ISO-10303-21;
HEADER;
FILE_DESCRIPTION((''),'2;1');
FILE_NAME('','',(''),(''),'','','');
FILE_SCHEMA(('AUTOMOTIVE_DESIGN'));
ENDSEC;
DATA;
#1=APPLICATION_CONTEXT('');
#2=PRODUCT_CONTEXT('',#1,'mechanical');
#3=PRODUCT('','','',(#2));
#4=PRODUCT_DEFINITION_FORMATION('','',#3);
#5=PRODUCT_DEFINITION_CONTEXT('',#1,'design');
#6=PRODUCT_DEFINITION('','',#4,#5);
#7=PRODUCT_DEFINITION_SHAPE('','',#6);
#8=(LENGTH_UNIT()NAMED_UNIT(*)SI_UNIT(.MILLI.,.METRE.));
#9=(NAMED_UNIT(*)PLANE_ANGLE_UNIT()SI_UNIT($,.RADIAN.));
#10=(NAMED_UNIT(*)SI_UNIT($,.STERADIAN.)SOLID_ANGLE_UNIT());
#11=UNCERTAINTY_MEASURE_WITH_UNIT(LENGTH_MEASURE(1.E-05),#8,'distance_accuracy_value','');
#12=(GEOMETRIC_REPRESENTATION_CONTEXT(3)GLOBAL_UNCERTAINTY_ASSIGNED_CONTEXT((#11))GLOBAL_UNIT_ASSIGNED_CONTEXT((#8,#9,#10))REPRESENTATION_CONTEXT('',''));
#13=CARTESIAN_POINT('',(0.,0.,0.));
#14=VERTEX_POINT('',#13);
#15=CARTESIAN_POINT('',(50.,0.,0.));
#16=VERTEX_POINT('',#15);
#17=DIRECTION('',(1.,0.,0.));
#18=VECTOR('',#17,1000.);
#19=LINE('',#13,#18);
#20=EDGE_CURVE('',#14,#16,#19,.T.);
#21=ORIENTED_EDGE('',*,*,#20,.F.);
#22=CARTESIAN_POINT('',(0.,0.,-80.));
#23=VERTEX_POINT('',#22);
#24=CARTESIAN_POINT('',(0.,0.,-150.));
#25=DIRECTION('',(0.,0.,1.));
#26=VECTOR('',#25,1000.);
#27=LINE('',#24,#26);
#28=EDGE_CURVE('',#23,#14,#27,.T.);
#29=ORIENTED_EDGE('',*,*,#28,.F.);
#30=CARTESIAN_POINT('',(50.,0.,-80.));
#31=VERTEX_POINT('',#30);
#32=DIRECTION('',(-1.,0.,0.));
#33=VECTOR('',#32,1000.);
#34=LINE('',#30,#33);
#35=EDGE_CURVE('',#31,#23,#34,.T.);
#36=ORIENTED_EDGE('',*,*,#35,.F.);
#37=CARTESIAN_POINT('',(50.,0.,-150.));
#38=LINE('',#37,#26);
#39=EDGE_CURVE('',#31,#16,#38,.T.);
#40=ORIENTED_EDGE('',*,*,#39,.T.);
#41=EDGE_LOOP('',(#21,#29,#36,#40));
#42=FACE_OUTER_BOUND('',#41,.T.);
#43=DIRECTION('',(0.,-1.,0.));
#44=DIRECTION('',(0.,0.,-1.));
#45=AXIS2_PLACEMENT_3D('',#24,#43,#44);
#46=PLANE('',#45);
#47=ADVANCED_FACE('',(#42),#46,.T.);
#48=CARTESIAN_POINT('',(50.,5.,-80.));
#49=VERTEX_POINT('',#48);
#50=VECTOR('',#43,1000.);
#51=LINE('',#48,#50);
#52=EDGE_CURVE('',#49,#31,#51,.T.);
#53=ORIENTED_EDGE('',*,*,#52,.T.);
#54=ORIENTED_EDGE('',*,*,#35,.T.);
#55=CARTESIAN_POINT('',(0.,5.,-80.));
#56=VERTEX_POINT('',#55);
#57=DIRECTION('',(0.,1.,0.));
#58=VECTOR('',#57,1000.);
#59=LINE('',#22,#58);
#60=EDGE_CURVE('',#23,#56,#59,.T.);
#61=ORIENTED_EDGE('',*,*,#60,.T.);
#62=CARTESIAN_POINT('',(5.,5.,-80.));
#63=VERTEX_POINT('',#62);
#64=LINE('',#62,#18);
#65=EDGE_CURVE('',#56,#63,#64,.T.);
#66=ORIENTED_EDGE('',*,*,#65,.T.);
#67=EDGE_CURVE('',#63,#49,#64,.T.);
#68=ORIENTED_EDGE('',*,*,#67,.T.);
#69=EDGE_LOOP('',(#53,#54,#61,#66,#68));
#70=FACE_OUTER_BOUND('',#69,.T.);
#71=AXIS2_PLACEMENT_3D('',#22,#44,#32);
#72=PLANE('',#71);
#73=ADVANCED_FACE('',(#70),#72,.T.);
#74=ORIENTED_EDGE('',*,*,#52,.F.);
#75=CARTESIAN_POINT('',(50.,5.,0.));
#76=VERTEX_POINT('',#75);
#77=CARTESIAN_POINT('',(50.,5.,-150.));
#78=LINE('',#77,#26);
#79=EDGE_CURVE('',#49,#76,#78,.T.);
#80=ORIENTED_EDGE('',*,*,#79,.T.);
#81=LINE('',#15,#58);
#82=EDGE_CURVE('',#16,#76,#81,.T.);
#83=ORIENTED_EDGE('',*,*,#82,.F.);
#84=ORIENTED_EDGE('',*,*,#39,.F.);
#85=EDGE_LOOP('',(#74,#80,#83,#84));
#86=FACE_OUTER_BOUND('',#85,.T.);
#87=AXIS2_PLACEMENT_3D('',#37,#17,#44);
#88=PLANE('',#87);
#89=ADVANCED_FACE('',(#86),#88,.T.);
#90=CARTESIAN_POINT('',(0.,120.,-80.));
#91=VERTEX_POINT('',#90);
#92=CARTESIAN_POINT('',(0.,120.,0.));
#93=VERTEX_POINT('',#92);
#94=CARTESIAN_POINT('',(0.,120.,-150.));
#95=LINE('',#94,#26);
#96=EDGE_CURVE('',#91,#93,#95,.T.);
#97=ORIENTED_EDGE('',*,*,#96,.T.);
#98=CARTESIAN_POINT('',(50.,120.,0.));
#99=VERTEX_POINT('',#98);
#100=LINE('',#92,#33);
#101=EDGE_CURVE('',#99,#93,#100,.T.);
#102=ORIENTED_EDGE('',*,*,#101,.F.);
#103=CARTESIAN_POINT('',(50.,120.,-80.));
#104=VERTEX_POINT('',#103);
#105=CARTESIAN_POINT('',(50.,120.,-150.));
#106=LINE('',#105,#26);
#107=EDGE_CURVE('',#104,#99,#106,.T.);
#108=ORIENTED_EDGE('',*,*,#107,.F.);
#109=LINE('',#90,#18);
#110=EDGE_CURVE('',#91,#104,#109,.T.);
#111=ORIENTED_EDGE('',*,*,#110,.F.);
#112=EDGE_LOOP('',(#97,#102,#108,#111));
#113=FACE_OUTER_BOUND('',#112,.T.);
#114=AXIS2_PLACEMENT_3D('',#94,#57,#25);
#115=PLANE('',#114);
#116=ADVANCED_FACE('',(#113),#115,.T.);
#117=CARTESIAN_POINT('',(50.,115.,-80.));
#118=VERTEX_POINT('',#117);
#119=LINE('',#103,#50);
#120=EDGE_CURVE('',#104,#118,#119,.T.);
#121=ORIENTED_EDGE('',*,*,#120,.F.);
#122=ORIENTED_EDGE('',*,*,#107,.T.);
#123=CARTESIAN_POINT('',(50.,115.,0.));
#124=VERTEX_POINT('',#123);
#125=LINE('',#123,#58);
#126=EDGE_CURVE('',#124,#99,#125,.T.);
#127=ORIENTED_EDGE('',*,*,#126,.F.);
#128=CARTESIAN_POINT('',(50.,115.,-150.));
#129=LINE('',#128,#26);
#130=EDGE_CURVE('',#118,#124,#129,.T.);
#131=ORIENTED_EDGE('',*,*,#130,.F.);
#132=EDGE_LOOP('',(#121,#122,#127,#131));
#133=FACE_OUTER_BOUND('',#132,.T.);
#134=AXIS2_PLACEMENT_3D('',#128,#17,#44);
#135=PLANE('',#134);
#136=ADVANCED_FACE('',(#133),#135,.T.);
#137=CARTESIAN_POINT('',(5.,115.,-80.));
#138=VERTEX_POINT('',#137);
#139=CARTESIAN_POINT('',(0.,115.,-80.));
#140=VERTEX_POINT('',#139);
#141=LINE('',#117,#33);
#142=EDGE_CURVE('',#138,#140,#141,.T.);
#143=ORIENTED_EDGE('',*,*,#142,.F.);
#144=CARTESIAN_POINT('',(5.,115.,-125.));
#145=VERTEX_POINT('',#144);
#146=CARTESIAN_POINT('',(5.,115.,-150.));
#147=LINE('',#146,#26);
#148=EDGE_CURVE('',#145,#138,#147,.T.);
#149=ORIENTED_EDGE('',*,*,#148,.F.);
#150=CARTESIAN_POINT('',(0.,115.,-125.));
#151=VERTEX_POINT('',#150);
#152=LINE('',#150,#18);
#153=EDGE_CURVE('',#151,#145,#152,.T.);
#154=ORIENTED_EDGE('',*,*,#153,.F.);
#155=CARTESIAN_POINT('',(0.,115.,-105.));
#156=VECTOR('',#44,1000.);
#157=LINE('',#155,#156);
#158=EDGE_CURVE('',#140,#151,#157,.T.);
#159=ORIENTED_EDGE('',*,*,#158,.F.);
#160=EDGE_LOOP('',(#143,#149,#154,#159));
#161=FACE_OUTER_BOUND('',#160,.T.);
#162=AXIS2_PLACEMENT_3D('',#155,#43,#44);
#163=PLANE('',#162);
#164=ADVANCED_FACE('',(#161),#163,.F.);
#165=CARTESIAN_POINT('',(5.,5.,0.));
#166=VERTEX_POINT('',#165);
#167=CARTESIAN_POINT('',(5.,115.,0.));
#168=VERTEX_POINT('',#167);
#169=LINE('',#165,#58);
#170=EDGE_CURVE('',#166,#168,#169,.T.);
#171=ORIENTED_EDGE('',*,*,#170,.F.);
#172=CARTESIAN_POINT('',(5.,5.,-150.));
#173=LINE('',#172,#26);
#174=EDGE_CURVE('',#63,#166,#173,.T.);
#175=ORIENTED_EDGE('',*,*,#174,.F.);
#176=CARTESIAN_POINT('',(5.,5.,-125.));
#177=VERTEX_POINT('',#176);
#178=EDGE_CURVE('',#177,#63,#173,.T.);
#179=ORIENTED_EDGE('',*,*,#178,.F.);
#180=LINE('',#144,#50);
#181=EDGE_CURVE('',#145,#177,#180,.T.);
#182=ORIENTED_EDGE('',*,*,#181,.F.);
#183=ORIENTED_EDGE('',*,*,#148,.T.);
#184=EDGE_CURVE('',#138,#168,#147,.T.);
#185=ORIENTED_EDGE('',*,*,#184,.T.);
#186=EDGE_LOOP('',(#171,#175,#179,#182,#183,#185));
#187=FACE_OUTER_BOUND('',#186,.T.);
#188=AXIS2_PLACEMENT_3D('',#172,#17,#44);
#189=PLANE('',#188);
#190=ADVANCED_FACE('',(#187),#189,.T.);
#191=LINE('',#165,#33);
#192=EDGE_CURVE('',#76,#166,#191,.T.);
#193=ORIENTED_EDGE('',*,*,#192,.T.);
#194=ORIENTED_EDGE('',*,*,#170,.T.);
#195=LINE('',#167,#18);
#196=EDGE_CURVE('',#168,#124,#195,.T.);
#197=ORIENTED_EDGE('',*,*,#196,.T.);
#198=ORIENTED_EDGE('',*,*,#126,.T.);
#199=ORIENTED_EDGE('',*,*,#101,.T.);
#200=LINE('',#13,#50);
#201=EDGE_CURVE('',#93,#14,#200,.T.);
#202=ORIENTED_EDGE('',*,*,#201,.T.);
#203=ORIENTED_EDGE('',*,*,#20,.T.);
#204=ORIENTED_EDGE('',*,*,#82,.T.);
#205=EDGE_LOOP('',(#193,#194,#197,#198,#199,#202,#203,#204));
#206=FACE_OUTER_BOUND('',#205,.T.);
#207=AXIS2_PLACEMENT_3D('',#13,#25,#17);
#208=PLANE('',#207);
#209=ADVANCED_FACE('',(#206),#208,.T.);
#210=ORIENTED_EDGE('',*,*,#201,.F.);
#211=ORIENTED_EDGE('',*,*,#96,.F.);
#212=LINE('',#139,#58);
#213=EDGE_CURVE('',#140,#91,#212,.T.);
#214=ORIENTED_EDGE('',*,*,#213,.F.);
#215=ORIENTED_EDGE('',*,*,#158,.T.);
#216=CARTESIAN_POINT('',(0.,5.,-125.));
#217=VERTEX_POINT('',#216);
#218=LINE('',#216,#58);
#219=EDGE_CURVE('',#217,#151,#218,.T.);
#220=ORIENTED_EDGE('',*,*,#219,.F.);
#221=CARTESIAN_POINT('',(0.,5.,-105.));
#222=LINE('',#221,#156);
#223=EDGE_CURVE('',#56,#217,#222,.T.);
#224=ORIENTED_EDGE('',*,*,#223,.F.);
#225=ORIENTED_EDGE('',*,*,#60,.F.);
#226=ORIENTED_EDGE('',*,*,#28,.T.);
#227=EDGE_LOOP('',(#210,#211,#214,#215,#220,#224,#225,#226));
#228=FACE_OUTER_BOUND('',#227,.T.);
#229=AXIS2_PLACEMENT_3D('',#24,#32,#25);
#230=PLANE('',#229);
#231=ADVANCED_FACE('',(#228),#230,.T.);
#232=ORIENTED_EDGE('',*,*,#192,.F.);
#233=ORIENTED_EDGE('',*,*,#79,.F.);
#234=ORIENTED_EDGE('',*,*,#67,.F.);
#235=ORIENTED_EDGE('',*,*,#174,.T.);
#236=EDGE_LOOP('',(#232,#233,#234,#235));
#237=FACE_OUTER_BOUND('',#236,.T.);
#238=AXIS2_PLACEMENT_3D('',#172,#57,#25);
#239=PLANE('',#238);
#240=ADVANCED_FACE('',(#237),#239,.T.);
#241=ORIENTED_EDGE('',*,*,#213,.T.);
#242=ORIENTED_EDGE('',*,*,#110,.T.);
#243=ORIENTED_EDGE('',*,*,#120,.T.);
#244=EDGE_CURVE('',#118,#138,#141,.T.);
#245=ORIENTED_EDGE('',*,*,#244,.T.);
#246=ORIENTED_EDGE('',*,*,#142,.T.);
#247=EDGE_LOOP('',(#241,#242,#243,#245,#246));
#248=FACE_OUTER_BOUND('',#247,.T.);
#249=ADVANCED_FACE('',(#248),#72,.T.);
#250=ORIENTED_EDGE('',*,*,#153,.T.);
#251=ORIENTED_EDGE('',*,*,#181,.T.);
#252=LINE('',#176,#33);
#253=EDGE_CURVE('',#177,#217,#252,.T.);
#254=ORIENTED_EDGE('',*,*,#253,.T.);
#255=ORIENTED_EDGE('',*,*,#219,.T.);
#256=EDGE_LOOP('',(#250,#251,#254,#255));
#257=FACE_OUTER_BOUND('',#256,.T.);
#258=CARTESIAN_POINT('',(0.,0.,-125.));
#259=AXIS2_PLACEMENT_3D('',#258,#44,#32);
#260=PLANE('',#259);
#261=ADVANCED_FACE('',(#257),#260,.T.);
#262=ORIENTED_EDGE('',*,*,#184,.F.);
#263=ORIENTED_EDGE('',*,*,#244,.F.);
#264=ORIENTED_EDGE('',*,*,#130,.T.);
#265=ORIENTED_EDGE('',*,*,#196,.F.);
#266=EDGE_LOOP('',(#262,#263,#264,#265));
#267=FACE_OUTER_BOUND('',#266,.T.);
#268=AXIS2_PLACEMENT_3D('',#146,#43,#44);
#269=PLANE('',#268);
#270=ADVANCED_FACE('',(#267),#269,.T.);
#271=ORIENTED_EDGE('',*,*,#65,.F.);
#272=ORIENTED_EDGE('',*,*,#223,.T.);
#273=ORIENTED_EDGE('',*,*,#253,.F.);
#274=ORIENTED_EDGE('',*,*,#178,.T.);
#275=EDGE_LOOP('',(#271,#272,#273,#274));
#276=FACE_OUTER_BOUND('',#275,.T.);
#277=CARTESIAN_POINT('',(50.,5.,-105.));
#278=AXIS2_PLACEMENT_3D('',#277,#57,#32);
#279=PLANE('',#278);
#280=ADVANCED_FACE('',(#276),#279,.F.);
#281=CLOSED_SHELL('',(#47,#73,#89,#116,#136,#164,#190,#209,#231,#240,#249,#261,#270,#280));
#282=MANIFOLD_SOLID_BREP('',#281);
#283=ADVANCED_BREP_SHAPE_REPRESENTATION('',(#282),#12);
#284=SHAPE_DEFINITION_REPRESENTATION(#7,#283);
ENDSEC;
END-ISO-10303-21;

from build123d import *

# Parameters (mm, degrees)
EXTRUDE_1_DEPTH     = 150
SKETCH_2_W          = 50
SKETCH_2_H          = 5
CUT_EXTRUDE_1_DEPTH = 45
SKETCH_3_W          = 5
SKETCH_3_H          = 110
CUT_EXTRUDE_2_DEPTH = 25
CUT_EXTRUDE_3_DEPTH = 25
CUT_EXTRUDE_4_DEPTH = 25


with BuildPart() as part:
    # 草图1 → 凸台-拉伸1 (new body)
    with BuildSketch(Plane.XY):
        Polygon((0, 0), (0, 120), (50, 120), (50, 115), (5, 115), (5, 5), (50, 5), (50, 0), align=None)
    extrude(amount=-EXTRUDE_1_DEPTH)

    # 草图2 → 切除-拉伸1 (cut)
    with BuildSketch(Plane(origin=(0, 0, -150), x_dir=(-1, 0, 0), z_dir=(0, 0, -1))):
        with Locations((-25, 117.5)):
            Rectangle(SKETCH_2_W, SKETCH_2_H)
        with Locations((-25, 2.5)):
            Rectangle(SKETCH_2_W, SKETCH_2_H)
    extrude(amount=-CUT_EXTRUDE_1_DEPTH, mode=Mode.SUBTRACT)

    # 草图3 → 切除-拉伸2 (cut)
    with BuildSketch(Plane(origin=(0, 0, -150), x_dir=(-1, 0, 0), z_dir=(0, 0, -1))):
        with Locations((-2.5, 60)):
            Rectangle(SKETCH_3_W, SKETCH_3_H)
    extrude(amount=-CUT_EXTRUDE_2_DEPTH, mode=Mode.SUBTRACT)

    # 草图4 → 切除-拉伸3 (cut)
    with BuildSketch(Plane(origin=(0, 0, -105), x_dir=(-1, 0, 0), z_dir=(0, 0, -1))):
        Polygon((-50, 120), (-50, 115), (-5, 115), (0, 115), (0, 120), align=None)
    extrude(amount=-CUT_EXTRUDE_3_DEPTH, mode=Mode.SUBTRACT)

    # 草图5 → 切除-拉伸4 (cut)
    with BuildSketch(Plane(origin=(0, 0, -105), x_dir=(-1, 0, 0), z_dir=(0, 0, -1))):
        Polygon((-50, 5), (-50, 0), (0, 0), (0, 5), (-5, 5), align=None)
    extrude(amount=-CUT_EXTRUDE_4_DEPTH, mode=Mode.SUBTRACT)


solid = part.part
